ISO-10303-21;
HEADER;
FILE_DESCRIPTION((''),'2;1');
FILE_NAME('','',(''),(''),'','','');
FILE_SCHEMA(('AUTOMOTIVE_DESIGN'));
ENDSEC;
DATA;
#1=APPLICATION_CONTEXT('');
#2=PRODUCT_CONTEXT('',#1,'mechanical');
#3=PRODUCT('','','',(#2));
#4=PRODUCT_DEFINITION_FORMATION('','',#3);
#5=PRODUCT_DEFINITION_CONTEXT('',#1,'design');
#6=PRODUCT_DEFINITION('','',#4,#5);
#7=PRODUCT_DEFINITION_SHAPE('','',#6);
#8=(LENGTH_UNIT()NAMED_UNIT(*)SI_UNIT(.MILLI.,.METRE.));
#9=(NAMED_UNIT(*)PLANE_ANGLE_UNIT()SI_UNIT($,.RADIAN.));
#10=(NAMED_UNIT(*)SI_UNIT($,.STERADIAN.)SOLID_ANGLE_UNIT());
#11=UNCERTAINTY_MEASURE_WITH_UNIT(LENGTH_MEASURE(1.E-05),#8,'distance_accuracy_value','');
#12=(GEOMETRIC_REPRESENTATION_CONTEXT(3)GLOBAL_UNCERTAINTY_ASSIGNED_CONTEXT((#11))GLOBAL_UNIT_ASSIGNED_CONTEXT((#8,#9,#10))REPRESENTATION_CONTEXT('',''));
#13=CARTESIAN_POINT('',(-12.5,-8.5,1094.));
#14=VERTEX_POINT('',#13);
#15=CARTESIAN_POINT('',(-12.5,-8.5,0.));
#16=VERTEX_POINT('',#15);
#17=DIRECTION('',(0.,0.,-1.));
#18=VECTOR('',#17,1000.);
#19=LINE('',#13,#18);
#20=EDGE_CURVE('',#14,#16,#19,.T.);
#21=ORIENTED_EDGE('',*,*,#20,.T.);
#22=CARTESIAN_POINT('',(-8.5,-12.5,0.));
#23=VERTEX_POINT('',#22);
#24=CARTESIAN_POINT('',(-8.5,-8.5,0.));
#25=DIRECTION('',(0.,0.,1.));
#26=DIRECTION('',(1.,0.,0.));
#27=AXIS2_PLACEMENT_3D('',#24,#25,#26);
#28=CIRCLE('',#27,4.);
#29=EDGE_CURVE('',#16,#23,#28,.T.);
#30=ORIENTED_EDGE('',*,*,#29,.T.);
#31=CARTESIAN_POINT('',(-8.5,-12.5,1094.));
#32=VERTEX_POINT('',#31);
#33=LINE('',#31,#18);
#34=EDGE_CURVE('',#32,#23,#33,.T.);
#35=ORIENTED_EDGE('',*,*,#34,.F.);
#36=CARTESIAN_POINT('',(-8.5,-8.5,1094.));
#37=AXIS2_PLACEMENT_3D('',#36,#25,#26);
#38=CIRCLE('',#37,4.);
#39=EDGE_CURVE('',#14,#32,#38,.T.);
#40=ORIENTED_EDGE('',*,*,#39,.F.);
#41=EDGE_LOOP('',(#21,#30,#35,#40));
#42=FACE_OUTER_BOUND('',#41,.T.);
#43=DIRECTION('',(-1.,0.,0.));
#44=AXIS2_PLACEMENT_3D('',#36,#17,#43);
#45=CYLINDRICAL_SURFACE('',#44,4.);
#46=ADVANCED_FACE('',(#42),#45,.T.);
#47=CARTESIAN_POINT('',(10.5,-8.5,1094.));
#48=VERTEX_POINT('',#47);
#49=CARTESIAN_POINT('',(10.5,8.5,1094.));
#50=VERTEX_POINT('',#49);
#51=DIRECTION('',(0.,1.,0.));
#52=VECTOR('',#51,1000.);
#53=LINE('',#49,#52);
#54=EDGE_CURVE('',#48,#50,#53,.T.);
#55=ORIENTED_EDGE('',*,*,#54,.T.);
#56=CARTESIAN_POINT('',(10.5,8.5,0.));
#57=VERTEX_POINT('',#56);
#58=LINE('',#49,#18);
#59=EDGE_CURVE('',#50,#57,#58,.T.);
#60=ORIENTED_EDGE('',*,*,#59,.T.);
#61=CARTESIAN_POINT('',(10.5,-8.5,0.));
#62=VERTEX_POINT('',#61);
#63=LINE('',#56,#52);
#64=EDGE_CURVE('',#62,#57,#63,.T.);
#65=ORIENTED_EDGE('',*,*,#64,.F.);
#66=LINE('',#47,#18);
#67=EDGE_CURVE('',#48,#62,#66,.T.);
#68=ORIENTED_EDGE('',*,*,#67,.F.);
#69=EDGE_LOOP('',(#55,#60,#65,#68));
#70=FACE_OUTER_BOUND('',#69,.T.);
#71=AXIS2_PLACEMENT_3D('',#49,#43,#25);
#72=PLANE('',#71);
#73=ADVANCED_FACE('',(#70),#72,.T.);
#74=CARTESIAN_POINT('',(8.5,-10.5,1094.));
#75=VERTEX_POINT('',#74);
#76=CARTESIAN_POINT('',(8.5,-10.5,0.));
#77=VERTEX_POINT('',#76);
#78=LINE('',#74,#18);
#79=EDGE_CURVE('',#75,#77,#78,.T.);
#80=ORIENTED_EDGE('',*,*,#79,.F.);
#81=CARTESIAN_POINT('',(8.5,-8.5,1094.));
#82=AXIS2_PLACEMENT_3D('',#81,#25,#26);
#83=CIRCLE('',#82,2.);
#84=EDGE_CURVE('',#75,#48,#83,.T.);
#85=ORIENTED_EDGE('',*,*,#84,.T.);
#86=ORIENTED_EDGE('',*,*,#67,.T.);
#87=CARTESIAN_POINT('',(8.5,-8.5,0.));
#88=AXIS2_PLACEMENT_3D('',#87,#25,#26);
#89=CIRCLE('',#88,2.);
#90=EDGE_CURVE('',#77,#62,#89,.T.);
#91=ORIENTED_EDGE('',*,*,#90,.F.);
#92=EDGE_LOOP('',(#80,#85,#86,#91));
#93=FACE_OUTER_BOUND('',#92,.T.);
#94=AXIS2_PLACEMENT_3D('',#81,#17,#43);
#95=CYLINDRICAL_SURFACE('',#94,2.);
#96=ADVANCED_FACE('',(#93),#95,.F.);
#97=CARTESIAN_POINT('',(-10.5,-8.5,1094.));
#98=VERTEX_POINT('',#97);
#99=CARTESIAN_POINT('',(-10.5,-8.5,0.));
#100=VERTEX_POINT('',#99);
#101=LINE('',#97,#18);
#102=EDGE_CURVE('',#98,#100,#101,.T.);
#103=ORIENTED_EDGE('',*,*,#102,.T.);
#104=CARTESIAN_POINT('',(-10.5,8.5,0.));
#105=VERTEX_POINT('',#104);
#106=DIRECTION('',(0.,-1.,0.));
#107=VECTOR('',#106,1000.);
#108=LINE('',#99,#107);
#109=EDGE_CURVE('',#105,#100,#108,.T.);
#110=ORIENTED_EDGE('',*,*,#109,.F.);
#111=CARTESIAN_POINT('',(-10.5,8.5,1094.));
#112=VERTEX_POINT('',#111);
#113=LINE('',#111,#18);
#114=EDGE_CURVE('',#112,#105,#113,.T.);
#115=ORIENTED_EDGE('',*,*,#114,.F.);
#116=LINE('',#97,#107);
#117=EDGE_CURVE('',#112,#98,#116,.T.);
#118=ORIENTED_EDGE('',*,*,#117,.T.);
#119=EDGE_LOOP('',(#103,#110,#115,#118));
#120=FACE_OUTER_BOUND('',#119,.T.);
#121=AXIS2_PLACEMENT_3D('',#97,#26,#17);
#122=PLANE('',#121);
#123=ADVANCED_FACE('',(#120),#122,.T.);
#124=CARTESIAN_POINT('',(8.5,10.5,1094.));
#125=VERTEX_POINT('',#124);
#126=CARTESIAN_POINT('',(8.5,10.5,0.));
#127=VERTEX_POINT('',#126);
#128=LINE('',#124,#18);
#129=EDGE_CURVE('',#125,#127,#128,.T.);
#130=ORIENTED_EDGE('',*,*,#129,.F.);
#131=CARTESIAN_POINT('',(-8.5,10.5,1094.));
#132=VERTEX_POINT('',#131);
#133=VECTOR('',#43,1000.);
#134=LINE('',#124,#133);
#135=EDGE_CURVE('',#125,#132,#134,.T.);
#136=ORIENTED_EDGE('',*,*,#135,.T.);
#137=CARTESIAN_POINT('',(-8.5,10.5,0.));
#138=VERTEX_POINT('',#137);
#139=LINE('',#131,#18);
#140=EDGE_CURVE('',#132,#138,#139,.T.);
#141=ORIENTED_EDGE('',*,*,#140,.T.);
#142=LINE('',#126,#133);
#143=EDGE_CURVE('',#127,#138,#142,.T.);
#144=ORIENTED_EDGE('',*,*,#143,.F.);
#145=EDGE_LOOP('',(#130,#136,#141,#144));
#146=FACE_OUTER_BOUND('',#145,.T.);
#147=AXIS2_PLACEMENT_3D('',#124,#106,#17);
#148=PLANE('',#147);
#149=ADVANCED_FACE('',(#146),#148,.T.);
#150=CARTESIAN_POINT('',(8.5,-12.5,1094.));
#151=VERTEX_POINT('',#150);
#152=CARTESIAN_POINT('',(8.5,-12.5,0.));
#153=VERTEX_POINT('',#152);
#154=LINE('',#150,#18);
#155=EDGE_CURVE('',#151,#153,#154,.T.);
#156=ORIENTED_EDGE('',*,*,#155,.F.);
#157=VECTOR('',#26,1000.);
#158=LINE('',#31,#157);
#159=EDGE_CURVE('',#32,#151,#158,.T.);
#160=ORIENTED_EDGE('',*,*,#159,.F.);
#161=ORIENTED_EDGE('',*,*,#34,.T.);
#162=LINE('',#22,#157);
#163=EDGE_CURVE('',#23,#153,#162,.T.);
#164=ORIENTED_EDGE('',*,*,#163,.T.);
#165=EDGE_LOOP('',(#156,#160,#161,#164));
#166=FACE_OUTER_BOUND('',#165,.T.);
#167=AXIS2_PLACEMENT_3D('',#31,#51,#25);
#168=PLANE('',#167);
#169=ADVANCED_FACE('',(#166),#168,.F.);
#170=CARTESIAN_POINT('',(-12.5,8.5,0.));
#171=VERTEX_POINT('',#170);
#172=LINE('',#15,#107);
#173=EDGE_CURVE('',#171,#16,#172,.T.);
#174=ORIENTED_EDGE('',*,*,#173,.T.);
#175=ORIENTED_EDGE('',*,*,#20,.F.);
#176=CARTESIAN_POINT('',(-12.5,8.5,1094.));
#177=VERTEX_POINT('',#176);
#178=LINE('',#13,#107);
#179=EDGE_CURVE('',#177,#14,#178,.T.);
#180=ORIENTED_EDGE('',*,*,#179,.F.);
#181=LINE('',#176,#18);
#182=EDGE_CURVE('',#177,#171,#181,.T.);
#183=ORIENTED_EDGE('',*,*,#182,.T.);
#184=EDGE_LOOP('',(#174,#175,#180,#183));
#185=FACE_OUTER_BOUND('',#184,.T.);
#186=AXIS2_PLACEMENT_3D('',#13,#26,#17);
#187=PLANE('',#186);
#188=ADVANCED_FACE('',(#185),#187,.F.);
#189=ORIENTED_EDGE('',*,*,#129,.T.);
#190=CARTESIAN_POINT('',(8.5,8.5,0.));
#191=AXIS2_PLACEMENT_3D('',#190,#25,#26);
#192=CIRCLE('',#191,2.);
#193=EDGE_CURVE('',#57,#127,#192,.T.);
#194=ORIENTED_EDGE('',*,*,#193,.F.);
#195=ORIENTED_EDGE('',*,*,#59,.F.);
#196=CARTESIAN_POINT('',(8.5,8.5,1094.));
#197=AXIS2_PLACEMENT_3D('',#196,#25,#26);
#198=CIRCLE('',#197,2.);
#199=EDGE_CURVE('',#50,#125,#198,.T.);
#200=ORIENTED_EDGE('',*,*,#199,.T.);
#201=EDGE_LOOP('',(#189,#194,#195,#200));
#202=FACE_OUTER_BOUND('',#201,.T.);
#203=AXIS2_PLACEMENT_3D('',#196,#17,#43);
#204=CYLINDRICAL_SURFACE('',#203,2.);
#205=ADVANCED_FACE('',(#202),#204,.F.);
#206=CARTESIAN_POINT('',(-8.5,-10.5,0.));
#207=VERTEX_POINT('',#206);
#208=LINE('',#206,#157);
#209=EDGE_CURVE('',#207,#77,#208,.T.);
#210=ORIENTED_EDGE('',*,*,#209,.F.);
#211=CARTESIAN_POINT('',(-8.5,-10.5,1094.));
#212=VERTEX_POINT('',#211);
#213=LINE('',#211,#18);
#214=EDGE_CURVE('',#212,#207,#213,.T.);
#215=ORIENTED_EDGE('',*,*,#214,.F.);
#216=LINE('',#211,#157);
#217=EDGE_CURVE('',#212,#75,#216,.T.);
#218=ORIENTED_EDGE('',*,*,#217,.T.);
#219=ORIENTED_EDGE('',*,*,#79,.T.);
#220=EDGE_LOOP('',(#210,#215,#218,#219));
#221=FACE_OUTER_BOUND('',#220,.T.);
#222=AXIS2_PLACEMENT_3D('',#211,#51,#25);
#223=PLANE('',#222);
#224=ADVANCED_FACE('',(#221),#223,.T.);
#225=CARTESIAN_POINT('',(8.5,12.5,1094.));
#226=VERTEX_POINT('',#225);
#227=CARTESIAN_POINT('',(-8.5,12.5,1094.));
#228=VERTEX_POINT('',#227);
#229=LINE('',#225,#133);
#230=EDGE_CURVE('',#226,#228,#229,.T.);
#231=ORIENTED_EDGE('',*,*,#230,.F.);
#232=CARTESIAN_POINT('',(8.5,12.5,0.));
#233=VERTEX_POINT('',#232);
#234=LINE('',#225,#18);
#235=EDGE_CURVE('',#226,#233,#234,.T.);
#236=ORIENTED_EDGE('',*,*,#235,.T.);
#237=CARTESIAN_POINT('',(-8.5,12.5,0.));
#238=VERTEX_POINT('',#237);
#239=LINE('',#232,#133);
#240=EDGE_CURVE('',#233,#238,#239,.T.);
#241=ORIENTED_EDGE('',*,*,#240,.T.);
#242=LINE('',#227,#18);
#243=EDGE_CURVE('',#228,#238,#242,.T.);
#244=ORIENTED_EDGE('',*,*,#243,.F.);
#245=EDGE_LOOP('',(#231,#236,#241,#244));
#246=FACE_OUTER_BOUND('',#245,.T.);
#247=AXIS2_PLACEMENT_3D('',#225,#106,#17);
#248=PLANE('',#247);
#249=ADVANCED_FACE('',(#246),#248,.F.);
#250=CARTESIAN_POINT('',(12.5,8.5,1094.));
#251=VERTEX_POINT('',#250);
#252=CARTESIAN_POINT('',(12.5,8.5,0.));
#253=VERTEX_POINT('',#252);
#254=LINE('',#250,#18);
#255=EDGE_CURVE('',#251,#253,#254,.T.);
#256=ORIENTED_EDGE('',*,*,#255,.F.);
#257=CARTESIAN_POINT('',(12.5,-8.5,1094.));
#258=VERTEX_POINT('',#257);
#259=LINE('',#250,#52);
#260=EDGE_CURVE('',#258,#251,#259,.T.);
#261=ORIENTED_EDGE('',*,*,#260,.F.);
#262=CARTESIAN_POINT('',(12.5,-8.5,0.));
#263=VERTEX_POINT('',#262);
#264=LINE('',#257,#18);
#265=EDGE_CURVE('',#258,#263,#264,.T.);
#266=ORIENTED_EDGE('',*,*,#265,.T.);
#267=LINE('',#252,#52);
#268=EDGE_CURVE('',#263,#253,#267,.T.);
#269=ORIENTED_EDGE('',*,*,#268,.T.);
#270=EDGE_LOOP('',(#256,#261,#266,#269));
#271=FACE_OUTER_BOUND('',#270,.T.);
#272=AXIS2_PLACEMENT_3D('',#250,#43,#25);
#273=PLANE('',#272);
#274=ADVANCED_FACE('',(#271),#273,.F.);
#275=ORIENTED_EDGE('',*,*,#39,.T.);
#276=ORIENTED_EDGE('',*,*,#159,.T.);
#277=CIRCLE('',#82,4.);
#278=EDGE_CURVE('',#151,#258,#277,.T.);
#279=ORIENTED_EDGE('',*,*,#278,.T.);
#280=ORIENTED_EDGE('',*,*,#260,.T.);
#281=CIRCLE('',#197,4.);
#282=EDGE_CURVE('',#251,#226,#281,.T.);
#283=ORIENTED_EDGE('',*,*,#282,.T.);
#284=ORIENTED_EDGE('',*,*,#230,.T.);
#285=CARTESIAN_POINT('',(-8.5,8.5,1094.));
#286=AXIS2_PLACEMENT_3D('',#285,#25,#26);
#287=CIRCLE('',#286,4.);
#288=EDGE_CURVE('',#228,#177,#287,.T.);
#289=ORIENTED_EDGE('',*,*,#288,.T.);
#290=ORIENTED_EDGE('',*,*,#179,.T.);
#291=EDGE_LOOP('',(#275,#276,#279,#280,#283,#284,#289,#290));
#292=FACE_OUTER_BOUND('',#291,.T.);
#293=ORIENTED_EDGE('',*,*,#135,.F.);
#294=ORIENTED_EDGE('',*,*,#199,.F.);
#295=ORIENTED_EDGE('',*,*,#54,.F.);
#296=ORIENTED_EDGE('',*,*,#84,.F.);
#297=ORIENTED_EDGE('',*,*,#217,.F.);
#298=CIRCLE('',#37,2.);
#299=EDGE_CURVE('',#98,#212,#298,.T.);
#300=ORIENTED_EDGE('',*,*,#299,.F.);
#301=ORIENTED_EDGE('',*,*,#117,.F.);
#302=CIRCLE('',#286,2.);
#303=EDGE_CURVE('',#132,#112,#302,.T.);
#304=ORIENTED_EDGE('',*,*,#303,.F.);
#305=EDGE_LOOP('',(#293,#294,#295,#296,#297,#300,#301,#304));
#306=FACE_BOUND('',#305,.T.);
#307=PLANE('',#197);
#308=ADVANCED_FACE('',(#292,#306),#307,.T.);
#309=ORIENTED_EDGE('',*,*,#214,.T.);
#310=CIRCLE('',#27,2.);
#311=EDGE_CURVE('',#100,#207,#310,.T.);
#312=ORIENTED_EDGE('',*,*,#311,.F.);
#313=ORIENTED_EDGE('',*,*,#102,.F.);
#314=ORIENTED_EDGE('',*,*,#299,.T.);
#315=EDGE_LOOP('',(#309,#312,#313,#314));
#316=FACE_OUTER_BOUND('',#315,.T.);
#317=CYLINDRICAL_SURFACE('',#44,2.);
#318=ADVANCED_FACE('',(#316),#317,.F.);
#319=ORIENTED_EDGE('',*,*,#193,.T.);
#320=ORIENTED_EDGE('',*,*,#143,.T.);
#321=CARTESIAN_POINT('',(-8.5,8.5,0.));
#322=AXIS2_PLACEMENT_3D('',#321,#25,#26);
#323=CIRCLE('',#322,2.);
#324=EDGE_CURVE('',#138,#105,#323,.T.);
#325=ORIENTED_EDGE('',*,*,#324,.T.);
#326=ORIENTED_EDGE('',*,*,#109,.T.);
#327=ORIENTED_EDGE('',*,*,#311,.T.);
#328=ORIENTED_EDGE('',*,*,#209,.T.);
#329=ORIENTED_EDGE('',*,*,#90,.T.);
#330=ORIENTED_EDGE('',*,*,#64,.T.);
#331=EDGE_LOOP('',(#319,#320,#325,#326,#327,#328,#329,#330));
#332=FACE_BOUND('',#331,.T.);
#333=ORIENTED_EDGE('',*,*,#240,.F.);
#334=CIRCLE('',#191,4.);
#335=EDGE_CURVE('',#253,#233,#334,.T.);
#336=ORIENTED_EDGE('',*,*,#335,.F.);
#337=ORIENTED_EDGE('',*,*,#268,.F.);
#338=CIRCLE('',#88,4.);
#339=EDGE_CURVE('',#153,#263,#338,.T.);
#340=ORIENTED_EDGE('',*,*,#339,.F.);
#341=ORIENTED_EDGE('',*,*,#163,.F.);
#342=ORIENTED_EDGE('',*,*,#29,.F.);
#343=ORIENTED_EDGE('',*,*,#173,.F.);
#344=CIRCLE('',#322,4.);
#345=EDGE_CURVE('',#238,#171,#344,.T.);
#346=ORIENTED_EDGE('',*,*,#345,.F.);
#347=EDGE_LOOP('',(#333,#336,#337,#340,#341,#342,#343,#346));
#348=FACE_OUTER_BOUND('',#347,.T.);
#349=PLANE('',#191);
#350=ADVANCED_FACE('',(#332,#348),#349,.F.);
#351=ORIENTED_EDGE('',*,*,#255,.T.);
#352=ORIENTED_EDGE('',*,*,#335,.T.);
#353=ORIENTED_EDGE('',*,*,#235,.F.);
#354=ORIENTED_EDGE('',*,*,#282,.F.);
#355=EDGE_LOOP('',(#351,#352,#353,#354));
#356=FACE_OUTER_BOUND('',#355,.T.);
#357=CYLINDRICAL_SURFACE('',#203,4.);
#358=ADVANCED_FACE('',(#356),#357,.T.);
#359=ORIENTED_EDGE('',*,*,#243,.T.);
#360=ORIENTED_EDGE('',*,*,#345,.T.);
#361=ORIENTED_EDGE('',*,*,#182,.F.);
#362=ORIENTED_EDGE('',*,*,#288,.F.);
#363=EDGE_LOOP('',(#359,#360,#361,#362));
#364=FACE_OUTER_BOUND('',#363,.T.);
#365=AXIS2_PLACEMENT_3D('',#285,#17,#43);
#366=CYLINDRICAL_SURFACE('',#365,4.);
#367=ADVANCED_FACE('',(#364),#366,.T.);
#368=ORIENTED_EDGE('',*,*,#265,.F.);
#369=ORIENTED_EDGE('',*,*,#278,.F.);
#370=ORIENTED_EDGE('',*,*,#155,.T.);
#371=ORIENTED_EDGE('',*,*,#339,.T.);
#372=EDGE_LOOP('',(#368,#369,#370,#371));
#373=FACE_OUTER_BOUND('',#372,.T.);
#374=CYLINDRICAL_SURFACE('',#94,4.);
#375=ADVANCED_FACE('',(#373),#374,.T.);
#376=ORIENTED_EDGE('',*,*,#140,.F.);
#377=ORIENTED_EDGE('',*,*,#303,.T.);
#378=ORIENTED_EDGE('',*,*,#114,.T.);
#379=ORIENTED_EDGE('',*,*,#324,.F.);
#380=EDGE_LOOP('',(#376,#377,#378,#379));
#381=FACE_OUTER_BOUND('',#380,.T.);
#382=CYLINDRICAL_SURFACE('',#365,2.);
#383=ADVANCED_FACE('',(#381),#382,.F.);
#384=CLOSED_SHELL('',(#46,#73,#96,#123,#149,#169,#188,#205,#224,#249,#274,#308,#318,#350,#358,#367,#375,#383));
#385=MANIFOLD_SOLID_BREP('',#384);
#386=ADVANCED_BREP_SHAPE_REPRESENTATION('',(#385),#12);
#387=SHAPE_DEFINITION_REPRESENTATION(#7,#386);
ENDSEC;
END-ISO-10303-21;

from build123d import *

# Parameters (mm, degrees)
BOSS_EXTRUDE1_DEPTH = 1094


with BuildPart() as part:
    # Sketch1 → Boss-Extrude1 (new body)
    with BuildSketch(Plane.XY):
        with BuildLine():
            Line((-8.5, -12.5), (8.5, -12.5))
            ThreePointArc((8.5, -12.5), (11.328427125, -11.328427125), (12.5, -8.5))
            Line((12.5, -8.5), (12.5, 8.5))
            ThreePointArc((12.5, 8.5), (11.328427125, 11.328427125), (8.5, 12.5))
            Line((8.5, 12.5), (-8.5, 12.5))
            ThreePointArc((-8.5, 12.5), (-11.328427125, 11.328427125), (-12.5, 8.5))
            Line((-12.5, 8.5), (-12.5, -8.5))
            ThreePointArc((-12.5, -8.5), (-11.328427125, -11.328427125), (-8.5, -12.5))
        make_face()
        with BuildLine():
            Line((-8.5, -10.5), (8.5, -10.5))
            ThreePointArc((8.5, -10.5), (9.914213562, -9.914213562), (10.5, -8.5))
            Line((10.5, -8.5), (10.5, 8.5))
            ThreePointArc((10.5, 8.5), (9.914213562, 9.914213562), (8.5, 10.5))
            Line((8.5, 10.5), (-8.5, 10.5))
            ThreePointArc((-8.5, 10.5), (-9.914213562, 9.914213562), (-10.5, 8.5))
            Line((-10.5, 8.5), (-10.5, -8.5))
            ThreePointArc((-10.5, -8.5), (-9.914213562, -9.914213562), (-8.5, -10.5))
        make_face(mode=Mode.SUBTRACT)
    extrude(amount=BOSS_EXTRUDE1_DEPTH)


solid = part.part
